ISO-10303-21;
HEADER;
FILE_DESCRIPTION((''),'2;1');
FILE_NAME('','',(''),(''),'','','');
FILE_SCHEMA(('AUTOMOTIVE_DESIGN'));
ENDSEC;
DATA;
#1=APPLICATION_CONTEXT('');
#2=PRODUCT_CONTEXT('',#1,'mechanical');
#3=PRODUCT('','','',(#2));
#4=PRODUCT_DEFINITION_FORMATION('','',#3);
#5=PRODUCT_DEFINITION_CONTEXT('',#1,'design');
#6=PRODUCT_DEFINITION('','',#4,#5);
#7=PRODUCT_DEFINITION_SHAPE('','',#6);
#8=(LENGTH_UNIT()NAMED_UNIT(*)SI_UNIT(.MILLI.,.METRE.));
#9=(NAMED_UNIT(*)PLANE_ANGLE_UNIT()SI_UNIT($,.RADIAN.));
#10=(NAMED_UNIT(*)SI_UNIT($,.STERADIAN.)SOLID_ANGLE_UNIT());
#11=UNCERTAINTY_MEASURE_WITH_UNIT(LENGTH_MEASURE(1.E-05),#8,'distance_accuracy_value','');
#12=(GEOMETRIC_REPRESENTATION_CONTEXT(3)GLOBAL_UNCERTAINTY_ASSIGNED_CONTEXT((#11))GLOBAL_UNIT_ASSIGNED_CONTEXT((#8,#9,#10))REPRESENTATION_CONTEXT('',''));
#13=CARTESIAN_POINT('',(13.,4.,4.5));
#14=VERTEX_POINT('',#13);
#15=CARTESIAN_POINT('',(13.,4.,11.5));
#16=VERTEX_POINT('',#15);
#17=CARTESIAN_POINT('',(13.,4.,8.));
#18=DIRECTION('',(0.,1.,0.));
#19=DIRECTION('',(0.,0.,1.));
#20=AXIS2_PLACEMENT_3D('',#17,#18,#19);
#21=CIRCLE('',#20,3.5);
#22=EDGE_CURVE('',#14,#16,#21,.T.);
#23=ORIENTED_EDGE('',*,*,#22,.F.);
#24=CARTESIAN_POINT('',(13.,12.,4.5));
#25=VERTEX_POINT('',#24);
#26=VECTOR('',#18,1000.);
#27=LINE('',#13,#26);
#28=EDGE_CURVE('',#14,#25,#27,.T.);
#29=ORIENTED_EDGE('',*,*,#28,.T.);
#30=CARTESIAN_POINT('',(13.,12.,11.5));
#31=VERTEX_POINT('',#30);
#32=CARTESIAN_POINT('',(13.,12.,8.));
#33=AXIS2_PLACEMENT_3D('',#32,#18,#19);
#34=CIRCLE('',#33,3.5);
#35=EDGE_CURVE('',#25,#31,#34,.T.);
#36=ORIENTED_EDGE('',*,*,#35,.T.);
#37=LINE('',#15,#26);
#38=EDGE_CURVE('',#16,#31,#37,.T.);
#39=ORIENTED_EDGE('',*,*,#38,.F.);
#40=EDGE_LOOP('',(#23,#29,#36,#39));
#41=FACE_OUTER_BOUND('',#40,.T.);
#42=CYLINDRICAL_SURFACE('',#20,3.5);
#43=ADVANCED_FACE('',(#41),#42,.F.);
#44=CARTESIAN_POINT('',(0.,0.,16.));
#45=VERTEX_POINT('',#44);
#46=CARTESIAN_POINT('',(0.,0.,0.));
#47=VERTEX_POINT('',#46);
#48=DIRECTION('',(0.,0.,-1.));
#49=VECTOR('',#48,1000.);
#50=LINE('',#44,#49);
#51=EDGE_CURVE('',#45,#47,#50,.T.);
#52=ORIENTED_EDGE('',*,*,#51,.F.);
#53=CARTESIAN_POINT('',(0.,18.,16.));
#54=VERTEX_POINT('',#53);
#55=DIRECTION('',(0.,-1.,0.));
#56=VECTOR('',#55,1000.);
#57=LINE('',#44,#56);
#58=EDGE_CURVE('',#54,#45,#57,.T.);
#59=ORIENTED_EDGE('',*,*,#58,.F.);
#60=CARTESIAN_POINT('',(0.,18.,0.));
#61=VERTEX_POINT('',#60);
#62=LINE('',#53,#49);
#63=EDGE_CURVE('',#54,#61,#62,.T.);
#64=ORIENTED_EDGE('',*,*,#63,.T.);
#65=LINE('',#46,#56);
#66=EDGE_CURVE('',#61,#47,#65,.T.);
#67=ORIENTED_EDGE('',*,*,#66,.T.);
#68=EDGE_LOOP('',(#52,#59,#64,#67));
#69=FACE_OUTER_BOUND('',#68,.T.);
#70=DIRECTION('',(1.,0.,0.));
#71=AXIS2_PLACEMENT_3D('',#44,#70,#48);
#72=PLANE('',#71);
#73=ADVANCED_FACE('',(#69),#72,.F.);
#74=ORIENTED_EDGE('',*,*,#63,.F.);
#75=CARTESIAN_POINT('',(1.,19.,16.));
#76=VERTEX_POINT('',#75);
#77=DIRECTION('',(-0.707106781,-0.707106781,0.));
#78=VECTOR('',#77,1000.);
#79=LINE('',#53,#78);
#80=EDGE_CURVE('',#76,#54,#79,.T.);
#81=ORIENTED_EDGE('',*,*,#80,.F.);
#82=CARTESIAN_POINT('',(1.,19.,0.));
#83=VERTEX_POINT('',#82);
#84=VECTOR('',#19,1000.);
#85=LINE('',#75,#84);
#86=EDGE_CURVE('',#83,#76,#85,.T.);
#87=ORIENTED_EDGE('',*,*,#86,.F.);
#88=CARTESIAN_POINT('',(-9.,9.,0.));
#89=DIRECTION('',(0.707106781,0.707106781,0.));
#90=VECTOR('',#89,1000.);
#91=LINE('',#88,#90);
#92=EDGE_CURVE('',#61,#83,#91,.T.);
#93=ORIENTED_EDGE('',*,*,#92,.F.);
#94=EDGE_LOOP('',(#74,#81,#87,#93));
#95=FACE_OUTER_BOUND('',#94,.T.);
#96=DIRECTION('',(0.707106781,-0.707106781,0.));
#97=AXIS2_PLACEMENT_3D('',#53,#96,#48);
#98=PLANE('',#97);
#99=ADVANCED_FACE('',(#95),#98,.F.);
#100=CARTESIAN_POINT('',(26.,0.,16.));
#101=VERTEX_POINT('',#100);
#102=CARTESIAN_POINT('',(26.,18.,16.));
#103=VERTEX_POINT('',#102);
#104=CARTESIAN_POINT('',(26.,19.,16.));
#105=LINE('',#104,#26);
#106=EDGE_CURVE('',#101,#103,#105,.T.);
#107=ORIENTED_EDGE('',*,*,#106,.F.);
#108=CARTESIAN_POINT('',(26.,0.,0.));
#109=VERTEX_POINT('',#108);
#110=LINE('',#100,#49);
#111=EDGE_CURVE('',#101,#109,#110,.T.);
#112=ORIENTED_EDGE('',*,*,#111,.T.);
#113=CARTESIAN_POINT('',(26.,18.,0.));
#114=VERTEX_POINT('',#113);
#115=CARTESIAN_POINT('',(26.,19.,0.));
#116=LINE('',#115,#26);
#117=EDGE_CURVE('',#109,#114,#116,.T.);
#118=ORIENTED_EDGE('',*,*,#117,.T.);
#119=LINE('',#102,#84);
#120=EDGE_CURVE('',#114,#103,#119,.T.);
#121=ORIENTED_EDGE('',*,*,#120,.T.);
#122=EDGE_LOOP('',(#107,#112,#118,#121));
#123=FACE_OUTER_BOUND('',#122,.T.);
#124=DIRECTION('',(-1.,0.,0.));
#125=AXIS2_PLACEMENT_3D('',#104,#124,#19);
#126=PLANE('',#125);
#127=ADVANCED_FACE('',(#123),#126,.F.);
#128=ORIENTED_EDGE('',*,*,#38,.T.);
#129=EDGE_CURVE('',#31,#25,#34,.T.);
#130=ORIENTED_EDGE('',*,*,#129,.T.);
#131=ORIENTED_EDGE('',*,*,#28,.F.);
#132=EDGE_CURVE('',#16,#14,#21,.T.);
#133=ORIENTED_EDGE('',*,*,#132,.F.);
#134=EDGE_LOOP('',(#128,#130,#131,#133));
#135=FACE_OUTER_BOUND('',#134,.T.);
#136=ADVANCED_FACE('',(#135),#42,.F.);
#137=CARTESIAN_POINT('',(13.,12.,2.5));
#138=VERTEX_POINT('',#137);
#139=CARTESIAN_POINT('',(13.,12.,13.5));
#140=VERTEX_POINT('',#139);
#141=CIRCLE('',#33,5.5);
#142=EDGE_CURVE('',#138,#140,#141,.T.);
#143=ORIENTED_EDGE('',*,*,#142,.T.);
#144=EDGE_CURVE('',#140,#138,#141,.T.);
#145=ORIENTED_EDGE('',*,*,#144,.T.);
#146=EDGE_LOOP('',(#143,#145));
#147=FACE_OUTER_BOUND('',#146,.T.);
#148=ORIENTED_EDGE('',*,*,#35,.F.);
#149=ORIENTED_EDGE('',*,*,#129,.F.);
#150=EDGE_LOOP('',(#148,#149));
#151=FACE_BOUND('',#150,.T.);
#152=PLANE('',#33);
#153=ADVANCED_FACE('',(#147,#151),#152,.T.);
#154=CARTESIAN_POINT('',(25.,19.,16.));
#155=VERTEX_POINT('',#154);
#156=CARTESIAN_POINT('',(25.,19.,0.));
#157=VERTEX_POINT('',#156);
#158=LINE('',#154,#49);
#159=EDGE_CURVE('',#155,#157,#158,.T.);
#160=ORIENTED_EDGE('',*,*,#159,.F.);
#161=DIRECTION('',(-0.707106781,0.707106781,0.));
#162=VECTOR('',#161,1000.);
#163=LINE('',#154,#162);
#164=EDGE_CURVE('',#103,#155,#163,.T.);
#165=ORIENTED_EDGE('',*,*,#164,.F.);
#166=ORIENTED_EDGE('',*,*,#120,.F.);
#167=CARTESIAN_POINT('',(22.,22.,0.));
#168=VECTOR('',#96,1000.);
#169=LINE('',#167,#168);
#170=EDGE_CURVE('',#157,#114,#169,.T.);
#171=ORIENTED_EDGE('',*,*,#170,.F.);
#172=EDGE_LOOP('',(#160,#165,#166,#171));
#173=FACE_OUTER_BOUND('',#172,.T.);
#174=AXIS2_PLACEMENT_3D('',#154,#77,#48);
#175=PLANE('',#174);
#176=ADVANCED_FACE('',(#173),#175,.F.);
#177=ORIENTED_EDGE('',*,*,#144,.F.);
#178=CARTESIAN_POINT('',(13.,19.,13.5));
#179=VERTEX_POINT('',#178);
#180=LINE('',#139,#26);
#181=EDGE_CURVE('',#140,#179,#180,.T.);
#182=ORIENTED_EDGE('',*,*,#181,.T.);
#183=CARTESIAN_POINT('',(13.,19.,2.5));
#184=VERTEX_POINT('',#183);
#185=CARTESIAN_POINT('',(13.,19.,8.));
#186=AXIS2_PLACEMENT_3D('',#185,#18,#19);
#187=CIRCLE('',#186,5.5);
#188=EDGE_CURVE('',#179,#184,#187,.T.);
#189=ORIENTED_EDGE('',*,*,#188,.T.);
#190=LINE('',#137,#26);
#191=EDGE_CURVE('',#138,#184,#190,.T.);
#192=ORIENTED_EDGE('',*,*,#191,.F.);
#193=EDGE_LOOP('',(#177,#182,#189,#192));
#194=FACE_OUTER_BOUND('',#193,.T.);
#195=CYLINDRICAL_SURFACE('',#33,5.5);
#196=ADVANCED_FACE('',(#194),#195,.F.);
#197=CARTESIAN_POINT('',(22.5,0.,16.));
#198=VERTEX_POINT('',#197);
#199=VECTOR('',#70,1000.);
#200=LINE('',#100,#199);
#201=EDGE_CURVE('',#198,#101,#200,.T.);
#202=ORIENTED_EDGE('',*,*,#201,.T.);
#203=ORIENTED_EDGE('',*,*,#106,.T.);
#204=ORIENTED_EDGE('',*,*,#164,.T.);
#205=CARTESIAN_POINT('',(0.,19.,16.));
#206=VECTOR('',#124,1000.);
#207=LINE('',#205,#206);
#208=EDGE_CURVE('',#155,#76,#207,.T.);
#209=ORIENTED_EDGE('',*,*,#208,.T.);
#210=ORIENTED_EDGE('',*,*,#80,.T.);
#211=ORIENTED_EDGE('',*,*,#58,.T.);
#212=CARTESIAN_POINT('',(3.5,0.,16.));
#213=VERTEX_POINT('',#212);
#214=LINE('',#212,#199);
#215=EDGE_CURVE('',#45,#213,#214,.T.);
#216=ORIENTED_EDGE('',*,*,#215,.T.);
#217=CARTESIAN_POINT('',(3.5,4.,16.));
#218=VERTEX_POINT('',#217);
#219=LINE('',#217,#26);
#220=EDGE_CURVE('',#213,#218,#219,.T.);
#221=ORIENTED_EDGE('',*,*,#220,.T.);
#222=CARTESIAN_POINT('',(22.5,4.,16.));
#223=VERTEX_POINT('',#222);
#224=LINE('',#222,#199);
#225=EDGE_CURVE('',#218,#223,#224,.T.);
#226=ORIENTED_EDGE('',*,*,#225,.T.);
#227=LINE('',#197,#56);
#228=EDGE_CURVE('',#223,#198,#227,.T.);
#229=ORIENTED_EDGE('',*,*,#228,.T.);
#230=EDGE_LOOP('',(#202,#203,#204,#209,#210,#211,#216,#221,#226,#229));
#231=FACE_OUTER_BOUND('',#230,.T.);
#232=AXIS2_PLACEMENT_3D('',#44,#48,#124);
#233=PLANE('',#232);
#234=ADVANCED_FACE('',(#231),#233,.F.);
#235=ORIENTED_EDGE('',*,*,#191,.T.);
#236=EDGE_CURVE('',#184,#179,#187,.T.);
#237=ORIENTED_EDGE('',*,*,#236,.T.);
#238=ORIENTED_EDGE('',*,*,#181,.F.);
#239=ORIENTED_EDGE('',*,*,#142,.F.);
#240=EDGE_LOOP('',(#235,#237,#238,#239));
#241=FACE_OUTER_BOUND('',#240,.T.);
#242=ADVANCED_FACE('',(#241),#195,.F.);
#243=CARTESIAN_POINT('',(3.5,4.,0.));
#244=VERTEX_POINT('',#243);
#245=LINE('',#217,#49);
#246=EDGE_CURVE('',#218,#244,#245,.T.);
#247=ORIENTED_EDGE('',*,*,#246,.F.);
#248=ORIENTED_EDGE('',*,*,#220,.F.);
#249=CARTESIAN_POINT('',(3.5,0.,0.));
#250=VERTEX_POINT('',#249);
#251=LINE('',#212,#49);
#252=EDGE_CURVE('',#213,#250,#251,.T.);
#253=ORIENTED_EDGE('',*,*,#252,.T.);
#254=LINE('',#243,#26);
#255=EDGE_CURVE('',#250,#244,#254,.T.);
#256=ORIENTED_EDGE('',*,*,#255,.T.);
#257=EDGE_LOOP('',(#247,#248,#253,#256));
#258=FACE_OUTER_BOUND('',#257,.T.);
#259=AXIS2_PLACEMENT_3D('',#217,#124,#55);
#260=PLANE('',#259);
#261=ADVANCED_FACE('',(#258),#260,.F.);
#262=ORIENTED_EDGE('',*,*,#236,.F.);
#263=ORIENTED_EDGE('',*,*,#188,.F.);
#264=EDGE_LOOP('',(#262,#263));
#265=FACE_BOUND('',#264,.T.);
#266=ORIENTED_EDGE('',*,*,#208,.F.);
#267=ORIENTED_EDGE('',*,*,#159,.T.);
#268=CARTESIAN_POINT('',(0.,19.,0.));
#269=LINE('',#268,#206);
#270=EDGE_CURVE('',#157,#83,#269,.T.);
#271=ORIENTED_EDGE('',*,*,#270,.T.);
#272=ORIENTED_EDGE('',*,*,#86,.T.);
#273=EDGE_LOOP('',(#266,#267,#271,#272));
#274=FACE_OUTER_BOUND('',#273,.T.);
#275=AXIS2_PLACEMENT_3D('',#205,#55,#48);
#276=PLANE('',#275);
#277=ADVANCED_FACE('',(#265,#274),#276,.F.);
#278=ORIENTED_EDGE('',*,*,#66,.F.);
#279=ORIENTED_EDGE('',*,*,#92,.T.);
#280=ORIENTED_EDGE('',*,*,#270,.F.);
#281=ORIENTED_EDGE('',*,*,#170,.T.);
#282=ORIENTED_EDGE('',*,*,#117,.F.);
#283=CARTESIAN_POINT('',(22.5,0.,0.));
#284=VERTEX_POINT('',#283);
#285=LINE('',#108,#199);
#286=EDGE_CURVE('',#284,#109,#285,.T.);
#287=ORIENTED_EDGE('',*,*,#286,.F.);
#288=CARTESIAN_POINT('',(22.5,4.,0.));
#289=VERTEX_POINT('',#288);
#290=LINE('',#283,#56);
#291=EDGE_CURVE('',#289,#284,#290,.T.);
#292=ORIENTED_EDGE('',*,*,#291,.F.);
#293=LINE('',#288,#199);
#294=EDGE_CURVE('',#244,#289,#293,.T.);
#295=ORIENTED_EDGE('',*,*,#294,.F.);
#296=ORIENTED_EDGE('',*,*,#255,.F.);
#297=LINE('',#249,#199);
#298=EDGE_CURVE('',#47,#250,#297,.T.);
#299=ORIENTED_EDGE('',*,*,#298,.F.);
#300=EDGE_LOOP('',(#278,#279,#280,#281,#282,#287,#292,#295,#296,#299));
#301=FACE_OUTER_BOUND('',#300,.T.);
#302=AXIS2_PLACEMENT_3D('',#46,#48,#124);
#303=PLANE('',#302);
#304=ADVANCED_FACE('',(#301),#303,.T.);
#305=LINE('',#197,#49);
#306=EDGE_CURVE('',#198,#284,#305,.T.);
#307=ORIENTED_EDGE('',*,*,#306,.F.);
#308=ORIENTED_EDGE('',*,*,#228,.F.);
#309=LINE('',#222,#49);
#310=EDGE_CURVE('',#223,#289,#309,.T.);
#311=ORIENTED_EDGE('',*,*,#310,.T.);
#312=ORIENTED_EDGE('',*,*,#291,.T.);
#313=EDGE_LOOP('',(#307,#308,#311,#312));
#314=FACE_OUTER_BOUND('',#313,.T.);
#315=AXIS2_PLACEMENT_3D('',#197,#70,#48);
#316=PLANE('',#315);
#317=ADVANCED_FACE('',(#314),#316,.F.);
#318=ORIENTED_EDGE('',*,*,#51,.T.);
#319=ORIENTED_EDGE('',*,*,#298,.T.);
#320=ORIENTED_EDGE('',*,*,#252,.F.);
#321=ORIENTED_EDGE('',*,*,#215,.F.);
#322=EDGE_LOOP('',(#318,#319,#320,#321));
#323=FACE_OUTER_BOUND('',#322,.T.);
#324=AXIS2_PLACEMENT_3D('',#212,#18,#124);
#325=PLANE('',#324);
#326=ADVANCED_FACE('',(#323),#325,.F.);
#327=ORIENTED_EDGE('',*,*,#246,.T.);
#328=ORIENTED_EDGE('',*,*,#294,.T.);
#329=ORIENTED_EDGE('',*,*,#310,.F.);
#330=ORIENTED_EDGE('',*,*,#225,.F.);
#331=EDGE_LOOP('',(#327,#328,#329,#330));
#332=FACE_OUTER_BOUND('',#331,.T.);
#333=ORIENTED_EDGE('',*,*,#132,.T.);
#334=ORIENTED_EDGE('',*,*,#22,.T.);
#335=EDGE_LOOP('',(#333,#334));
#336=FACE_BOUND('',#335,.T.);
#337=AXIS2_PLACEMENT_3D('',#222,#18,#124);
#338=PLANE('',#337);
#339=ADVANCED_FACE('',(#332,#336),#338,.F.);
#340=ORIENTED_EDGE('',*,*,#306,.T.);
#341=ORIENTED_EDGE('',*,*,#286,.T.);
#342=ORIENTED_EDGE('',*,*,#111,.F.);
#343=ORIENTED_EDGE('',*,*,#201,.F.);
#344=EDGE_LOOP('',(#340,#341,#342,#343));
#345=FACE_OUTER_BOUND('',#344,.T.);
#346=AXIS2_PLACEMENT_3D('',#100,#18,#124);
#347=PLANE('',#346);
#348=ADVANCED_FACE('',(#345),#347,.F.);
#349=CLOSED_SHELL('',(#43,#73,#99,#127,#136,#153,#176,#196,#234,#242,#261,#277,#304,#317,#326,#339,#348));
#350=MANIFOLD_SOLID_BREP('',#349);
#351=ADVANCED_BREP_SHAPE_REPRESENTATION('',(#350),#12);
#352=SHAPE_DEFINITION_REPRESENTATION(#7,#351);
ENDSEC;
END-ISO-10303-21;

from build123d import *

# Parameters (mm, degrees)
BOSS_EXTRUDE1_DEPTH = 16
SKETCH2_R           = 5.5
CUT_EXTRUDE1_DEPTH  = 7
SKETCH3_R           = 3.5
CUT_EXTRUDE2_DEPTH  = 8
CHAMFER1_SIZE       = 1


with BuildPart() as part:
    # Sketch1 → Boss-Extrude1 (new body)
    with BuildSketch(Plane.XY):
        Polygon((0, 0), (0, 19), (26, 19), (26, 0), (22.5, 0), (22.5, 4), (3.5, 4), (3.5, 0), align=None)
    extrude(amount=BOSS_EXTRUDE1_DEPTH)

    # Sketch2 → Cut-Extrude1 (cut)
    with BuildSketch(Plane(origin=(0, 19, 0), x_dir=(1, 0, 0), z_dir=(0, 1, 0))):
        with Locations(Location((13, -8, 0), (0, 0, 270))):
            Circle(SKETCH2_R)
    extrude(amount=-CUT_EXTRUDE1_DEPTH, mode=Mode.SUBTRACT)

    # Sketch3 → Cut-Extrude2 (cut)
    with BuildSketch(Plane(origin=(0, 12, 0), x_dir=(1, 0, 0), z_dir=(0, 1, 0))):
        with Locations(Location((13, -8, 0), (0, 0, 270))):
            Circle(SKETCH3_R)
    extrude(amount=-CUT_EXTRUDE2_DEPTH, mode=Mode.SUBTRACT)

    # Chamfer1
    chamfer1_edges = [part.edges().sort_by_distance(p)[0] for p in [
        (0, 19, 8),
        (26, 19, 8),
    ]]
    chamfer(chamfer1_edges, length=CHAMFER1_SIZE)


solid = part.part
